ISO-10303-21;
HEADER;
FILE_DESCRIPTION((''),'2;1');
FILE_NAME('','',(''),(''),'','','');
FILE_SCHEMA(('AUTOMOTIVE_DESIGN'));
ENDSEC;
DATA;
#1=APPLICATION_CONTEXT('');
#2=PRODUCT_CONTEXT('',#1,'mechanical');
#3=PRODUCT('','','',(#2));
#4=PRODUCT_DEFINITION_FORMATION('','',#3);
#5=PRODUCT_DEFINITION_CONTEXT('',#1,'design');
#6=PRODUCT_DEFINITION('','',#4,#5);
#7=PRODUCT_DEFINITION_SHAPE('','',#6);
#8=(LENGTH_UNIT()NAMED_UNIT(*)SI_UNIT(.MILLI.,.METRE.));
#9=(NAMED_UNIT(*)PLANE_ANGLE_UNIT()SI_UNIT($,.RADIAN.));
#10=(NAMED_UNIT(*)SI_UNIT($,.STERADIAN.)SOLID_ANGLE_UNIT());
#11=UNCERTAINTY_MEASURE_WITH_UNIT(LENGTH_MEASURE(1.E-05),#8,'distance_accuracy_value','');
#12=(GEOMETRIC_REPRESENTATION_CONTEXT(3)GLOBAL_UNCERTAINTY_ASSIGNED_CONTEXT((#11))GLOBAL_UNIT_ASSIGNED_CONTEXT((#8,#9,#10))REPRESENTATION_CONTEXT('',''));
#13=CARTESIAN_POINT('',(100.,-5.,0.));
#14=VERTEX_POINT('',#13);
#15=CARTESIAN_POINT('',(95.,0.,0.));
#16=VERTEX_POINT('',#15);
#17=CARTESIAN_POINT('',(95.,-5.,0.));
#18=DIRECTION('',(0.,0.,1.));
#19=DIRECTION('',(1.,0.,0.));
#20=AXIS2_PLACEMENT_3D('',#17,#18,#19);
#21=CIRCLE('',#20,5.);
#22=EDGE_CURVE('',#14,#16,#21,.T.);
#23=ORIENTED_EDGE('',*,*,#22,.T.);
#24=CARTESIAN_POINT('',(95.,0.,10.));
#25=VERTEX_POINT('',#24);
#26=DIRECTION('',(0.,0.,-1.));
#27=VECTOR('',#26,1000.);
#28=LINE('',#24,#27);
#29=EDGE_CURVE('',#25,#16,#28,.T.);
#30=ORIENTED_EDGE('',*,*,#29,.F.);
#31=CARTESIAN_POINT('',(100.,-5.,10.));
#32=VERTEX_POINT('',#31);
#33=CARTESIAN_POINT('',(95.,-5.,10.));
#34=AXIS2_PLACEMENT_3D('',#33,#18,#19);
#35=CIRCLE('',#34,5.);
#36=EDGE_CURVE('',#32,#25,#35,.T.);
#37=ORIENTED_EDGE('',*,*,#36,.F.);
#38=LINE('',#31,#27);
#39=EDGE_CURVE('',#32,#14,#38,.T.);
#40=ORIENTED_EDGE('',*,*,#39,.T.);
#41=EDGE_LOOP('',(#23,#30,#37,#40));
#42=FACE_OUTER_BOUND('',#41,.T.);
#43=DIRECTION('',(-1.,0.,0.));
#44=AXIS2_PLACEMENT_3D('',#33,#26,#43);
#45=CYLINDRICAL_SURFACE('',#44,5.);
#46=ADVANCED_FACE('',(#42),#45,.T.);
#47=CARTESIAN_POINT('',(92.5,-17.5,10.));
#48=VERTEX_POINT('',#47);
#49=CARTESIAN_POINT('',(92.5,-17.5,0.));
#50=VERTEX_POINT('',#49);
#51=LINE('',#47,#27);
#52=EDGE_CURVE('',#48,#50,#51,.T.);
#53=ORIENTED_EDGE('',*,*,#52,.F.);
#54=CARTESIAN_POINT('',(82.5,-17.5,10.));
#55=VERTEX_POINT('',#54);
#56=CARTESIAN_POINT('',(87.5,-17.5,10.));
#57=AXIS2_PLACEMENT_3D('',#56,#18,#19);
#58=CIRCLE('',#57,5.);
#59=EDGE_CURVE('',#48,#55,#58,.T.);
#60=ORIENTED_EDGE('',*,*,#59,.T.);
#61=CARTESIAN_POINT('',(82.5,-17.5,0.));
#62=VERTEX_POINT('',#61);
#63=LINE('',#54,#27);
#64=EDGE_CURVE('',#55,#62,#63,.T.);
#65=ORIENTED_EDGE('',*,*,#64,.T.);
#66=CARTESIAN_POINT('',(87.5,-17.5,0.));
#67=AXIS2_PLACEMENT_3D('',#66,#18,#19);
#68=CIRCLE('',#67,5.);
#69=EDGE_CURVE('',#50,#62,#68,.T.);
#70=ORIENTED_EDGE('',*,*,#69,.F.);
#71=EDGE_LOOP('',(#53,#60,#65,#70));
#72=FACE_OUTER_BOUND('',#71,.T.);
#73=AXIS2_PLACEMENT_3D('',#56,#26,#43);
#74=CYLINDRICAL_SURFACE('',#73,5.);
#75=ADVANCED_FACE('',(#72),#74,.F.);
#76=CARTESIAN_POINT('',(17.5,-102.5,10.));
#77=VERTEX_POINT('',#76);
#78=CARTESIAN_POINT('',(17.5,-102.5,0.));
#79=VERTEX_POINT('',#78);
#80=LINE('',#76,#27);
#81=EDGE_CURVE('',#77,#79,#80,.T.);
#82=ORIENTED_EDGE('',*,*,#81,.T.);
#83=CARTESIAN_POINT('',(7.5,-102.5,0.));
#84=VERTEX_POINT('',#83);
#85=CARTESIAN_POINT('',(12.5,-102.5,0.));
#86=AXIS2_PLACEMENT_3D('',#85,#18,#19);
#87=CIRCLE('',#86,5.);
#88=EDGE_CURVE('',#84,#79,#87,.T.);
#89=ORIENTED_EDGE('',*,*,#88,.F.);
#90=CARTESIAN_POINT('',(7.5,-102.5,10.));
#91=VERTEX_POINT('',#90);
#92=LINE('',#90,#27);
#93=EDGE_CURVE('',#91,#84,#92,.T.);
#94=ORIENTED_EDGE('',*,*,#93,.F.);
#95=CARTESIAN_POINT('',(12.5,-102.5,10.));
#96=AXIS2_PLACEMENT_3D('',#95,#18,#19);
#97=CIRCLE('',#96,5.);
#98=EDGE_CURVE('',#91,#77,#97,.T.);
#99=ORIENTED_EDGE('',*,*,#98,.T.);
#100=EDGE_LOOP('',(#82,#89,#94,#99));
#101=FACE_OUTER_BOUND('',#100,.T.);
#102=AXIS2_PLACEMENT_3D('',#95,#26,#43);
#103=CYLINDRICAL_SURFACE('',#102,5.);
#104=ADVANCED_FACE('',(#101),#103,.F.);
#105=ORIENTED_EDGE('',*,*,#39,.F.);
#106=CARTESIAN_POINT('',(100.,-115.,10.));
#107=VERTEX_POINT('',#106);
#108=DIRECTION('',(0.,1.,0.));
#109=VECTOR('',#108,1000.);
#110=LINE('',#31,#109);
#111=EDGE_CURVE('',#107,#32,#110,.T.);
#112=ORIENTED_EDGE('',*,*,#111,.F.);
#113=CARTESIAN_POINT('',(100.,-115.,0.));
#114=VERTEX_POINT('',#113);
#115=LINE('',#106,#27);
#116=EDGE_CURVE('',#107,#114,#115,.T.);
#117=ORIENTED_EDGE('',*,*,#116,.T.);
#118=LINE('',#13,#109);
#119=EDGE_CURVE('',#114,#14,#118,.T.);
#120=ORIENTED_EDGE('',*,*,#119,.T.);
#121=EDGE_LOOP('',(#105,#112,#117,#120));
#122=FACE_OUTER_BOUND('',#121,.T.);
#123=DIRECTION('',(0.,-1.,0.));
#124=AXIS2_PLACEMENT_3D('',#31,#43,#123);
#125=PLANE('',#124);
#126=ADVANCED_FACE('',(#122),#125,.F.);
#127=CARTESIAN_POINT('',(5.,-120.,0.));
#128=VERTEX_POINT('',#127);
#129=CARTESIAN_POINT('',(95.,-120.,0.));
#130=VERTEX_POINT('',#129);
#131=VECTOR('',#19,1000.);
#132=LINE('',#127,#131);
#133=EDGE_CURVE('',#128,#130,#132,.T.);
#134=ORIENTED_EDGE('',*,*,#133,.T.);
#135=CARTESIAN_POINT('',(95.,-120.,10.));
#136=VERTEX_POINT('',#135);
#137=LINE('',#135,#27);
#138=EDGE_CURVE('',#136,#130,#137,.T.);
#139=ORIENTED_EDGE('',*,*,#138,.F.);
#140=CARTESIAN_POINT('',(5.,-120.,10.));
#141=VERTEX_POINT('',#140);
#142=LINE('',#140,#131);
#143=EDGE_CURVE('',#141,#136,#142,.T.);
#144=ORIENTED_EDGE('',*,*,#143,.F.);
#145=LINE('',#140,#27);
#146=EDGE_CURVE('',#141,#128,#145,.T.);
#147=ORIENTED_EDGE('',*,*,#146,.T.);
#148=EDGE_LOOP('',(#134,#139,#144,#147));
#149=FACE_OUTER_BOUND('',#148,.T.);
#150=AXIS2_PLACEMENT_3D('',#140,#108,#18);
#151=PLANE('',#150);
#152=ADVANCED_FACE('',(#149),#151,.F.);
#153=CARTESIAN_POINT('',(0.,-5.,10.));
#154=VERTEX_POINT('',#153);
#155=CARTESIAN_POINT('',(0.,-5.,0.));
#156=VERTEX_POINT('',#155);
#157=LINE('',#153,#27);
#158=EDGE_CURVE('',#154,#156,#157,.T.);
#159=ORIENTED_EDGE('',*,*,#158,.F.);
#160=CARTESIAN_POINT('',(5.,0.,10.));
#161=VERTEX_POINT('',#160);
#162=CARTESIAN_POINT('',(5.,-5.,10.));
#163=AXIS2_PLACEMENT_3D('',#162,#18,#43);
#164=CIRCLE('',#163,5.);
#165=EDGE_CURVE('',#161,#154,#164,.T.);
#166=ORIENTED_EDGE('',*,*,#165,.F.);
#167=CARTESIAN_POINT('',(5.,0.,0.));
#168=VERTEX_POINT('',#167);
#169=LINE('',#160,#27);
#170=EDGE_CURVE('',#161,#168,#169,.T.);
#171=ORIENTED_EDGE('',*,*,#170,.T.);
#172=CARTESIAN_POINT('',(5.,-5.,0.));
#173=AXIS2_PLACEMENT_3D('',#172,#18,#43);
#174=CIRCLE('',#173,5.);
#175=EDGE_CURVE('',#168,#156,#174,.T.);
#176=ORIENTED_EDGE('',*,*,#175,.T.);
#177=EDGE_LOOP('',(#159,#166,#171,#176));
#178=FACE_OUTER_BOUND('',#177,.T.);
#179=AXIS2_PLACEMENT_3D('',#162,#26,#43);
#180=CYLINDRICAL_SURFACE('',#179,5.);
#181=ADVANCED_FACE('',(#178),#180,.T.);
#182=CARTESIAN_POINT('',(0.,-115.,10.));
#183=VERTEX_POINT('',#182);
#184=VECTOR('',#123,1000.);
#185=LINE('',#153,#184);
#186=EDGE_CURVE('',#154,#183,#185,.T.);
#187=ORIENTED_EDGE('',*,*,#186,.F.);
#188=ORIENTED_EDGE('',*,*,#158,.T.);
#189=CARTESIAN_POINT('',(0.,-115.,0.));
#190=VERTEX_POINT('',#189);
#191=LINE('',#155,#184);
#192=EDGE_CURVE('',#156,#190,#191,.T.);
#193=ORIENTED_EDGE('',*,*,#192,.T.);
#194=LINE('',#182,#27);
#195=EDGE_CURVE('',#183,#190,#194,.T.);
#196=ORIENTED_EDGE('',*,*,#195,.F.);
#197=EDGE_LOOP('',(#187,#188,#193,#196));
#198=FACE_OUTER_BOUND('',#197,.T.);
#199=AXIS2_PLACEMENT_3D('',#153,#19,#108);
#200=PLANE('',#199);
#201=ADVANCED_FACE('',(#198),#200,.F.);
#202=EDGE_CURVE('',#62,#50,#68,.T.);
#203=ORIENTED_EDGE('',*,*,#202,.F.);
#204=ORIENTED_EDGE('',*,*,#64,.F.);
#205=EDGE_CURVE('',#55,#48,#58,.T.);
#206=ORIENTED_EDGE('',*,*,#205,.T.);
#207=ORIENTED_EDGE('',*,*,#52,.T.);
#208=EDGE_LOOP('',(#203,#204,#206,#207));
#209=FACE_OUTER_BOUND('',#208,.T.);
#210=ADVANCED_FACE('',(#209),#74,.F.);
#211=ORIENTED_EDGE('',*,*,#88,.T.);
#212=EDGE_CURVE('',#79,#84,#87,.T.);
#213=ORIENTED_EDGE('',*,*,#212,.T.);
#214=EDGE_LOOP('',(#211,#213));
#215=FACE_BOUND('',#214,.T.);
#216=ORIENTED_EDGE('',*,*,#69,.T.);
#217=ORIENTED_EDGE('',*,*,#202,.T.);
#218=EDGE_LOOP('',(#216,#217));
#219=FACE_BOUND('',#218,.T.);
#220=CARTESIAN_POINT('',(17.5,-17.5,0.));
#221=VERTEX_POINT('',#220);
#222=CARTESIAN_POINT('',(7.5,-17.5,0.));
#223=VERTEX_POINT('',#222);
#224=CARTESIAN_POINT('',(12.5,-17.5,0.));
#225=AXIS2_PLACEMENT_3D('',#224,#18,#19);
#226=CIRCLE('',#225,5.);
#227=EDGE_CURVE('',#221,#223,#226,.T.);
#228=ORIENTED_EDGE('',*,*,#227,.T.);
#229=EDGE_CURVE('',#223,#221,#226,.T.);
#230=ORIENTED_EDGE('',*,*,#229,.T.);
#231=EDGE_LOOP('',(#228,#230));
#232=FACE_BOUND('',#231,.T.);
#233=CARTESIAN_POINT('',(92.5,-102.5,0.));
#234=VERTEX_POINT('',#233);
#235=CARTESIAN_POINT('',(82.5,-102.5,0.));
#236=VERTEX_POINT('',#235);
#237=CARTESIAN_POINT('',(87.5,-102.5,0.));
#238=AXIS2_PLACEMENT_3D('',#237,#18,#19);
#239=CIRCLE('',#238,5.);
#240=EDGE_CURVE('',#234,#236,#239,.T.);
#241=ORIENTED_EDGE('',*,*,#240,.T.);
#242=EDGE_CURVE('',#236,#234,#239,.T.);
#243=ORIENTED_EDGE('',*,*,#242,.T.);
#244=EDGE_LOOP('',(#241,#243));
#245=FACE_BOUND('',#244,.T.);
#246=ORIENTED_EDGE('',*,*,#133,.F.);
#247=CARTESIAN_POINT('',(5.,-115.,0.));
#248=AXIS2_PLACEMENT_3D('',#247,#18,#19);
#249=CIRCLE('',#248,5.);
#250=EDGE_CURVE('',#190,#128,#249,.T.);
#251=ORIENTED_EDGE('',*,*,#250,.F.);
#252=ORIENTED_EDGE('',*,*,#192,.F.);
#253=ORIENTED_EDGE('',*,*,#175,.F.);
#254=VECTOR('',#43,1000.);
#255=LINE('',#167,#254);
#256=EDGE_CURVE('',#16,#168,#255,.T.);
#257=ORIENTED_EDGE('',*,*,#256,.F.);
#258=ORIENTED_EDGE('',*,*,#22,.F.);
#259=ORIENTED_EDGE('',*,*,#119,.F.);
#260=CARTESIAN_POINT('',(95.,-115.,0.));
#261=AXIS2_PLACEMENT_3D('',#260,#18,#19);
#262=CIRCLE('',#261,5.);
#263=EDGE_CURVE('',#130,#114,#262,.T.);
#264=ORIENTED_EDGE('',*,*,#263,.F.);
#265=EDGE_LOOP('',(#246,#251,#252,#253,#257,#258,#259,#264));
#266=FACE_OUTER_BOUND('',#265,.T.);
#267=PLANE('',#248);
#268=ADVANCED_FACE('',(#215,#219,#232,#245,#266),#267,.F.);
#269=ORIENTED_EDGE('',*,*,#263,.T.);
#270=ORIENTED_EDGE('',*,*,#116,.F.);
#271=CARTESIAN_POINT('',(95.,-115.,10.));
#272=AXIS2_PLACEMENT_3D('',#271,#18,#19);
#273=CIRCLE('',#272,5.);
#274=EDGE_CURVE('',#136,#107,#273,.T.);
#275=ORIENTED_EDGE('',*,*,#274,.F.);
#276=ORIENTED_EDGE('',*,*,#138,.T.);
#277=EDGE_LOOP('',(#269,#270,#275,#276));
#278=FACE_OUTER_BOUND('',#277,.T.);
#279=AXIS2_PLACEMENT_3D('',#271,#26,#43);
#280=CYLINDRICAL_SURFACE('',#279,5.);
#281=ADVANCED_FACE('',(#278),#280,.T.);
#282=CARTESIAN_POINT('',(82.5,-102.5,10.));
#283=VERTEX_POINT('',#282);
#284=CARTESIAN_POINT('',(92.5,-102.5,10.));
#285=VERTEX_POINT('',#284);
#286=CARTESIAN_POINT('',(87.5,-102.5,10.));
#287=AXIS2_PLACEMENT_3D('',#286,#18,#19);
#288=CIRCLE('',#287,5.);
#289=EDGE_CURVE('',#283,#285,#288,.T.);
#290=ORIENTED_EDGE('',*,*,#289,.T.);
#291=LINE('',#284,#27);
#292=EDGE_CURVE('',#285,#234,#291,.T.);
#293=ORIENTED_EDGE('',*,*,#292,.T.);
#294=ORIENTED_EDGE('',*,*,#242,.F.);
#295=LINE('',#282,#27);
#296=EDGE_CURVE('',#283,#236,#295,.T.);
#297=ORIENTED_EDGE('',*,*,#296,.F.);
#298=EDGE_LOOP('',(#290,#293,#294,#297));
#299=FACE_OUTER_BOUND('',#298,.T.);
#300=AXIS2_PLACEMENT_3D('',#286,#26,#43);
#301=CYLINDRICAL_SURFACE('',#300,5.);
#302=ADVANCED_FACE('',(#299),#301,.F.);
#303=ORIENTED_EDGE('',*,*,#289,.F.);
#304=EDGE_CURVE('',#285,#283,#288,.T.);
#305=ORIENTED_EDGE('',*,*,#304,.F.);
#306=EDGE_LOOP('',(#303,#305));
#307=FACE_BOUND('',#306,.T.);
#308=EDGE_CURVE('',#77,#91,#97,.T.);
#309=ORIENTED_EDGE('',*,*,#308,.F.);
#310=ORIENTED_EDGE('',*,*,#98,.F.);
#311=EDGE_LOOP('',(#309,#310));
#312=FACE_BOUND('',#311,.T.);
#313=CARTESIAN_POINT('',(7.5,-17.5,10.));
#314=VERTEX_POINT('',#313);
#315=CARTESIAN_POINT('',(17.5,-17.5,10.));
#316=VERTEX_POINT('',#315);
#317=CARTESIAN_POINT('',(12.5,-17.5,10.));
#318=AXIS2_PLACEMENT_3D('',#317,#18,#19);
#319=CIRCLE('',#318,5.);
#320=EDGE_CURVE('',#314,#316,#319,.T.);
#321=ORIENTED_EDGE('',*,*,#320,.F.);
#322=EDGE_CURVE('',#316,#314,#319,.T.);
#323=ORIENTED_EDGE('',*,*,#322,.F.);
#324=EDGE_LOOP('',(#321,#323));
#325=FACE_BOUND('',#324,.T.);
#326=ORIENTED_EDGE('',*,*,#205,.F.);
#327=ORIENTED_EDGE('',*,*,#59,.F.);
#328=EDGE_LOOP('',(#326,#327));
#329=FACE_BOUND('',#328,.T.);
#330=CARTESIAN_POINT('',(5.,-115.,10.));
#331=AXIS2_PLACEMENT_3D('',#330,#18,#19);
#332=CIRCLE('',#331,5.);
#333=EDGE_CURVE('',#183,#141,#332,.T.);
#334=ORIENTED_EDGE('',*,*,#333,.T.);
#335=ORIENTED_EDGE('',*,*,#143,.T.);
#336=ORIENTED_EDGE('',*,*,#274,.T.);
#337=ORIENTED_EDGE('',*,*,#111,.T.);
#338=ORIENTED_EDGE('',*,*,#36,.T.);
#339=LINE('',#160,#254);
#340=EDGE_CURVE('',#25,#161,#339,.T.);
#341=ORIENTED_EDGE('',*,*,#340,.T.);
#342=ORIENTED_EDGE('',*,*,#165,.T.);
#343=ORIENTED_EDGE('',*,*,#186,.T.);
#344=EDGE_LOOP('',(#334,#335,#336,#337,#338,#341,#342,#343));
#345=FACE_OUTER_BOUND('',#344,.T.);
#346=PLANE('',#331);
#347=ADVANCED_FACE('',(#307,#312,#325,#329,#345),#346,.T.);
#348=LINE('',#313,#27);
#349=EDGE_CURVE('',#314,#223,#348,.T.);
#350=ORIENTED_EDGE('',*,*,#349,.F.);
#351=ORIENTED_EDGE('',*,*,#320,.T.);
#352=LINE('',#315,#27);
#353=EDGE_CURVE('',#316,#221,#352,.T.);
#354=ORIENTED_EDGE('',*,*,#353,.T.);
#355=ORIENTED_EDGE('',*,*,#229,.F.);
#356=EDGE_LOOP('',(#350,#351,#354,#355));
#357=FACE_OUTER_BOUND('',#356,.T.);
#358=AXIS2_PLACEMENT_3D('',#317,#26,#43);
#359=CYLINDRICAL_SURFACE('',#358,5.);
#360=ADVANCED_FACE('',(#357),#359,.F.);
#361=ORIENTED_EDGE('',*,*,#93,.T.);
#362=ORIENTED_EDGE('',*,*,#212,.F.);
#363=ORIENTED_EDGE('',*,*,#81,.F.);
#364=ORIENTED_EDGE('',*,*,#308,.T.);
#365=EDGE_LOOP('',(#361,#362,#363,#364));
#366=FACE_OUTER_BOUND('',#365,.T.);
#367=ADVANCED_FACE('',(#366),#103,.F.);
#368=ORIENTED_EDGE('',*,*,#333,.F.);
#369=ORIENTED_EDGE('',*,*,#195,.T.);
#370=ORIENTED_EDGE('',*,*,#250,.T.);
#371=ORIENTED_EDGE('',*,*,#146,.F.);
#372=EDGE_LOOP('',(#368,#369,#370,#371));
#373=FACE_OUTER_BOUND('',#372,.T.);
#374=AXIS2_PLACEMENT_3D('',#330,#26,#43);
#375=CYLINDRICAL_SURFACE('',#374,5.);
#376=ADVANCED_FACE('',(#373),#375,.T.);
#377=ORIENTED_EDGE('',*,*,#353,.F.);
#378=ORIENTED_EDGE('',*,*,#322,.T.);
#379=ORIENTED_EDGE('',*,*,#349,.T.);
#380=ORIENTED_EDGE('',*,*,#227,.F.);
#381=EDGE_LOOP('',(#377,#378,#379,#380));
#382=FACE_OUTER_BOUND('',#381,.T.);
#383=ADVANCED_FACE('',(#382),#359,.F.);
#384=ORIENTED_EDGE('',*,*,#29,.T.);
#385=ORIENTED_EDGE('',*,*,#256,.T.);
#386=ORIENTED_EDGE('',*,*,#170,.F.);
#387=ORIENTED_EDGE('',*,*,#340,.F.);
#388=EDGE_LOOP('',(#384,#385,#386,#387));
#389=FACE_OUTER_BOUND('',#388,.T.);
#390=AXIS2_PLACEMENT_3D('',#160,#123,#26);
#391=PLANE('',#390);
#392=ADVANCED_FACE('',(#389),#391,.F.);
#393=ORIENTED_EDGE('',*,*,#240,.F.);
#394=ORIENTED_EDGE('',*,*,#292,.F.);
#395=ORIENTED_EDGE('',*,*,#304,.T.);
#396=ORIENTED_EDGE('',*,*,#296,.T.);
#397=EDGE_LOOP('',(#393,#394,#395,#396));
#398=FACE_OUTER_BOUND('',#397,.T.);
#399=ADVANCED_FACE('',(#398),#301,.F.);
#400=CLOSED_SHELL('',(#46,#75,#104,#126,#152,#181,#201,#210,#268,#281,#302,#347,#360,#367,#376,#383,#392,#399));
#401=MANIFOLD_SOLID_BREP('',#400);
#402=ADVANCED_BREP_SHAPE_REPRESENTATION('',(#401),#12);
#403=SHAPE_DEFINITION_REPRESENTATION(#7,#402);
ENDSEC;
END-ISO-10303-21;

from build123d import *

# Parameters (mm, degrees)
SKETCH1_R           = 5
BOSS_EXTRUDE1_DEPTH = 10


with BuildPart() as part:
    # Sketch1 → Boss-Extrude1 (new body)
    with BuildSketch(Plane.XY):
        with BuildLine():
            Line((5, 0), (95, 0))
            ThreePointArc((95, 0), (98.535533906, -1.464466094), (100, -5))
            Line((100, -5), (100, -115))
            ThreePointArc((100, -115), (98.535533906, -118.535533906), (95, -120))
            Line((95, -120), (5, -120))
            ThreePointArc((5, -120), (1.464466094, -118.535533906), (0, -115))
            Line((0, -115), (0, -5))
            ThreePointArc((0, -5), (1.464466094, -1.464466094), (5, 0))
        make_face()
        with Locations((12.5, -17.5)):
            Circle(SKETCH1_R, mode=Mode.SUBTRACT)
        with Locations((87.5, -17.5)):
            Circle(SKETCH1_R, mode=Mode.SUBTRACT)
        with Locations((87.5, -102.5)):
            Circle(SKETCH1_R, mode=Mode.SUBTRACT)
        with Locations((12.5, -102.5)):
            Circle(SKETCH1_R, mode=Mode.SUBTRACT)
    extrude(amount=BOSS_EXTRUDE1_DEPTH)


solid = part.part
